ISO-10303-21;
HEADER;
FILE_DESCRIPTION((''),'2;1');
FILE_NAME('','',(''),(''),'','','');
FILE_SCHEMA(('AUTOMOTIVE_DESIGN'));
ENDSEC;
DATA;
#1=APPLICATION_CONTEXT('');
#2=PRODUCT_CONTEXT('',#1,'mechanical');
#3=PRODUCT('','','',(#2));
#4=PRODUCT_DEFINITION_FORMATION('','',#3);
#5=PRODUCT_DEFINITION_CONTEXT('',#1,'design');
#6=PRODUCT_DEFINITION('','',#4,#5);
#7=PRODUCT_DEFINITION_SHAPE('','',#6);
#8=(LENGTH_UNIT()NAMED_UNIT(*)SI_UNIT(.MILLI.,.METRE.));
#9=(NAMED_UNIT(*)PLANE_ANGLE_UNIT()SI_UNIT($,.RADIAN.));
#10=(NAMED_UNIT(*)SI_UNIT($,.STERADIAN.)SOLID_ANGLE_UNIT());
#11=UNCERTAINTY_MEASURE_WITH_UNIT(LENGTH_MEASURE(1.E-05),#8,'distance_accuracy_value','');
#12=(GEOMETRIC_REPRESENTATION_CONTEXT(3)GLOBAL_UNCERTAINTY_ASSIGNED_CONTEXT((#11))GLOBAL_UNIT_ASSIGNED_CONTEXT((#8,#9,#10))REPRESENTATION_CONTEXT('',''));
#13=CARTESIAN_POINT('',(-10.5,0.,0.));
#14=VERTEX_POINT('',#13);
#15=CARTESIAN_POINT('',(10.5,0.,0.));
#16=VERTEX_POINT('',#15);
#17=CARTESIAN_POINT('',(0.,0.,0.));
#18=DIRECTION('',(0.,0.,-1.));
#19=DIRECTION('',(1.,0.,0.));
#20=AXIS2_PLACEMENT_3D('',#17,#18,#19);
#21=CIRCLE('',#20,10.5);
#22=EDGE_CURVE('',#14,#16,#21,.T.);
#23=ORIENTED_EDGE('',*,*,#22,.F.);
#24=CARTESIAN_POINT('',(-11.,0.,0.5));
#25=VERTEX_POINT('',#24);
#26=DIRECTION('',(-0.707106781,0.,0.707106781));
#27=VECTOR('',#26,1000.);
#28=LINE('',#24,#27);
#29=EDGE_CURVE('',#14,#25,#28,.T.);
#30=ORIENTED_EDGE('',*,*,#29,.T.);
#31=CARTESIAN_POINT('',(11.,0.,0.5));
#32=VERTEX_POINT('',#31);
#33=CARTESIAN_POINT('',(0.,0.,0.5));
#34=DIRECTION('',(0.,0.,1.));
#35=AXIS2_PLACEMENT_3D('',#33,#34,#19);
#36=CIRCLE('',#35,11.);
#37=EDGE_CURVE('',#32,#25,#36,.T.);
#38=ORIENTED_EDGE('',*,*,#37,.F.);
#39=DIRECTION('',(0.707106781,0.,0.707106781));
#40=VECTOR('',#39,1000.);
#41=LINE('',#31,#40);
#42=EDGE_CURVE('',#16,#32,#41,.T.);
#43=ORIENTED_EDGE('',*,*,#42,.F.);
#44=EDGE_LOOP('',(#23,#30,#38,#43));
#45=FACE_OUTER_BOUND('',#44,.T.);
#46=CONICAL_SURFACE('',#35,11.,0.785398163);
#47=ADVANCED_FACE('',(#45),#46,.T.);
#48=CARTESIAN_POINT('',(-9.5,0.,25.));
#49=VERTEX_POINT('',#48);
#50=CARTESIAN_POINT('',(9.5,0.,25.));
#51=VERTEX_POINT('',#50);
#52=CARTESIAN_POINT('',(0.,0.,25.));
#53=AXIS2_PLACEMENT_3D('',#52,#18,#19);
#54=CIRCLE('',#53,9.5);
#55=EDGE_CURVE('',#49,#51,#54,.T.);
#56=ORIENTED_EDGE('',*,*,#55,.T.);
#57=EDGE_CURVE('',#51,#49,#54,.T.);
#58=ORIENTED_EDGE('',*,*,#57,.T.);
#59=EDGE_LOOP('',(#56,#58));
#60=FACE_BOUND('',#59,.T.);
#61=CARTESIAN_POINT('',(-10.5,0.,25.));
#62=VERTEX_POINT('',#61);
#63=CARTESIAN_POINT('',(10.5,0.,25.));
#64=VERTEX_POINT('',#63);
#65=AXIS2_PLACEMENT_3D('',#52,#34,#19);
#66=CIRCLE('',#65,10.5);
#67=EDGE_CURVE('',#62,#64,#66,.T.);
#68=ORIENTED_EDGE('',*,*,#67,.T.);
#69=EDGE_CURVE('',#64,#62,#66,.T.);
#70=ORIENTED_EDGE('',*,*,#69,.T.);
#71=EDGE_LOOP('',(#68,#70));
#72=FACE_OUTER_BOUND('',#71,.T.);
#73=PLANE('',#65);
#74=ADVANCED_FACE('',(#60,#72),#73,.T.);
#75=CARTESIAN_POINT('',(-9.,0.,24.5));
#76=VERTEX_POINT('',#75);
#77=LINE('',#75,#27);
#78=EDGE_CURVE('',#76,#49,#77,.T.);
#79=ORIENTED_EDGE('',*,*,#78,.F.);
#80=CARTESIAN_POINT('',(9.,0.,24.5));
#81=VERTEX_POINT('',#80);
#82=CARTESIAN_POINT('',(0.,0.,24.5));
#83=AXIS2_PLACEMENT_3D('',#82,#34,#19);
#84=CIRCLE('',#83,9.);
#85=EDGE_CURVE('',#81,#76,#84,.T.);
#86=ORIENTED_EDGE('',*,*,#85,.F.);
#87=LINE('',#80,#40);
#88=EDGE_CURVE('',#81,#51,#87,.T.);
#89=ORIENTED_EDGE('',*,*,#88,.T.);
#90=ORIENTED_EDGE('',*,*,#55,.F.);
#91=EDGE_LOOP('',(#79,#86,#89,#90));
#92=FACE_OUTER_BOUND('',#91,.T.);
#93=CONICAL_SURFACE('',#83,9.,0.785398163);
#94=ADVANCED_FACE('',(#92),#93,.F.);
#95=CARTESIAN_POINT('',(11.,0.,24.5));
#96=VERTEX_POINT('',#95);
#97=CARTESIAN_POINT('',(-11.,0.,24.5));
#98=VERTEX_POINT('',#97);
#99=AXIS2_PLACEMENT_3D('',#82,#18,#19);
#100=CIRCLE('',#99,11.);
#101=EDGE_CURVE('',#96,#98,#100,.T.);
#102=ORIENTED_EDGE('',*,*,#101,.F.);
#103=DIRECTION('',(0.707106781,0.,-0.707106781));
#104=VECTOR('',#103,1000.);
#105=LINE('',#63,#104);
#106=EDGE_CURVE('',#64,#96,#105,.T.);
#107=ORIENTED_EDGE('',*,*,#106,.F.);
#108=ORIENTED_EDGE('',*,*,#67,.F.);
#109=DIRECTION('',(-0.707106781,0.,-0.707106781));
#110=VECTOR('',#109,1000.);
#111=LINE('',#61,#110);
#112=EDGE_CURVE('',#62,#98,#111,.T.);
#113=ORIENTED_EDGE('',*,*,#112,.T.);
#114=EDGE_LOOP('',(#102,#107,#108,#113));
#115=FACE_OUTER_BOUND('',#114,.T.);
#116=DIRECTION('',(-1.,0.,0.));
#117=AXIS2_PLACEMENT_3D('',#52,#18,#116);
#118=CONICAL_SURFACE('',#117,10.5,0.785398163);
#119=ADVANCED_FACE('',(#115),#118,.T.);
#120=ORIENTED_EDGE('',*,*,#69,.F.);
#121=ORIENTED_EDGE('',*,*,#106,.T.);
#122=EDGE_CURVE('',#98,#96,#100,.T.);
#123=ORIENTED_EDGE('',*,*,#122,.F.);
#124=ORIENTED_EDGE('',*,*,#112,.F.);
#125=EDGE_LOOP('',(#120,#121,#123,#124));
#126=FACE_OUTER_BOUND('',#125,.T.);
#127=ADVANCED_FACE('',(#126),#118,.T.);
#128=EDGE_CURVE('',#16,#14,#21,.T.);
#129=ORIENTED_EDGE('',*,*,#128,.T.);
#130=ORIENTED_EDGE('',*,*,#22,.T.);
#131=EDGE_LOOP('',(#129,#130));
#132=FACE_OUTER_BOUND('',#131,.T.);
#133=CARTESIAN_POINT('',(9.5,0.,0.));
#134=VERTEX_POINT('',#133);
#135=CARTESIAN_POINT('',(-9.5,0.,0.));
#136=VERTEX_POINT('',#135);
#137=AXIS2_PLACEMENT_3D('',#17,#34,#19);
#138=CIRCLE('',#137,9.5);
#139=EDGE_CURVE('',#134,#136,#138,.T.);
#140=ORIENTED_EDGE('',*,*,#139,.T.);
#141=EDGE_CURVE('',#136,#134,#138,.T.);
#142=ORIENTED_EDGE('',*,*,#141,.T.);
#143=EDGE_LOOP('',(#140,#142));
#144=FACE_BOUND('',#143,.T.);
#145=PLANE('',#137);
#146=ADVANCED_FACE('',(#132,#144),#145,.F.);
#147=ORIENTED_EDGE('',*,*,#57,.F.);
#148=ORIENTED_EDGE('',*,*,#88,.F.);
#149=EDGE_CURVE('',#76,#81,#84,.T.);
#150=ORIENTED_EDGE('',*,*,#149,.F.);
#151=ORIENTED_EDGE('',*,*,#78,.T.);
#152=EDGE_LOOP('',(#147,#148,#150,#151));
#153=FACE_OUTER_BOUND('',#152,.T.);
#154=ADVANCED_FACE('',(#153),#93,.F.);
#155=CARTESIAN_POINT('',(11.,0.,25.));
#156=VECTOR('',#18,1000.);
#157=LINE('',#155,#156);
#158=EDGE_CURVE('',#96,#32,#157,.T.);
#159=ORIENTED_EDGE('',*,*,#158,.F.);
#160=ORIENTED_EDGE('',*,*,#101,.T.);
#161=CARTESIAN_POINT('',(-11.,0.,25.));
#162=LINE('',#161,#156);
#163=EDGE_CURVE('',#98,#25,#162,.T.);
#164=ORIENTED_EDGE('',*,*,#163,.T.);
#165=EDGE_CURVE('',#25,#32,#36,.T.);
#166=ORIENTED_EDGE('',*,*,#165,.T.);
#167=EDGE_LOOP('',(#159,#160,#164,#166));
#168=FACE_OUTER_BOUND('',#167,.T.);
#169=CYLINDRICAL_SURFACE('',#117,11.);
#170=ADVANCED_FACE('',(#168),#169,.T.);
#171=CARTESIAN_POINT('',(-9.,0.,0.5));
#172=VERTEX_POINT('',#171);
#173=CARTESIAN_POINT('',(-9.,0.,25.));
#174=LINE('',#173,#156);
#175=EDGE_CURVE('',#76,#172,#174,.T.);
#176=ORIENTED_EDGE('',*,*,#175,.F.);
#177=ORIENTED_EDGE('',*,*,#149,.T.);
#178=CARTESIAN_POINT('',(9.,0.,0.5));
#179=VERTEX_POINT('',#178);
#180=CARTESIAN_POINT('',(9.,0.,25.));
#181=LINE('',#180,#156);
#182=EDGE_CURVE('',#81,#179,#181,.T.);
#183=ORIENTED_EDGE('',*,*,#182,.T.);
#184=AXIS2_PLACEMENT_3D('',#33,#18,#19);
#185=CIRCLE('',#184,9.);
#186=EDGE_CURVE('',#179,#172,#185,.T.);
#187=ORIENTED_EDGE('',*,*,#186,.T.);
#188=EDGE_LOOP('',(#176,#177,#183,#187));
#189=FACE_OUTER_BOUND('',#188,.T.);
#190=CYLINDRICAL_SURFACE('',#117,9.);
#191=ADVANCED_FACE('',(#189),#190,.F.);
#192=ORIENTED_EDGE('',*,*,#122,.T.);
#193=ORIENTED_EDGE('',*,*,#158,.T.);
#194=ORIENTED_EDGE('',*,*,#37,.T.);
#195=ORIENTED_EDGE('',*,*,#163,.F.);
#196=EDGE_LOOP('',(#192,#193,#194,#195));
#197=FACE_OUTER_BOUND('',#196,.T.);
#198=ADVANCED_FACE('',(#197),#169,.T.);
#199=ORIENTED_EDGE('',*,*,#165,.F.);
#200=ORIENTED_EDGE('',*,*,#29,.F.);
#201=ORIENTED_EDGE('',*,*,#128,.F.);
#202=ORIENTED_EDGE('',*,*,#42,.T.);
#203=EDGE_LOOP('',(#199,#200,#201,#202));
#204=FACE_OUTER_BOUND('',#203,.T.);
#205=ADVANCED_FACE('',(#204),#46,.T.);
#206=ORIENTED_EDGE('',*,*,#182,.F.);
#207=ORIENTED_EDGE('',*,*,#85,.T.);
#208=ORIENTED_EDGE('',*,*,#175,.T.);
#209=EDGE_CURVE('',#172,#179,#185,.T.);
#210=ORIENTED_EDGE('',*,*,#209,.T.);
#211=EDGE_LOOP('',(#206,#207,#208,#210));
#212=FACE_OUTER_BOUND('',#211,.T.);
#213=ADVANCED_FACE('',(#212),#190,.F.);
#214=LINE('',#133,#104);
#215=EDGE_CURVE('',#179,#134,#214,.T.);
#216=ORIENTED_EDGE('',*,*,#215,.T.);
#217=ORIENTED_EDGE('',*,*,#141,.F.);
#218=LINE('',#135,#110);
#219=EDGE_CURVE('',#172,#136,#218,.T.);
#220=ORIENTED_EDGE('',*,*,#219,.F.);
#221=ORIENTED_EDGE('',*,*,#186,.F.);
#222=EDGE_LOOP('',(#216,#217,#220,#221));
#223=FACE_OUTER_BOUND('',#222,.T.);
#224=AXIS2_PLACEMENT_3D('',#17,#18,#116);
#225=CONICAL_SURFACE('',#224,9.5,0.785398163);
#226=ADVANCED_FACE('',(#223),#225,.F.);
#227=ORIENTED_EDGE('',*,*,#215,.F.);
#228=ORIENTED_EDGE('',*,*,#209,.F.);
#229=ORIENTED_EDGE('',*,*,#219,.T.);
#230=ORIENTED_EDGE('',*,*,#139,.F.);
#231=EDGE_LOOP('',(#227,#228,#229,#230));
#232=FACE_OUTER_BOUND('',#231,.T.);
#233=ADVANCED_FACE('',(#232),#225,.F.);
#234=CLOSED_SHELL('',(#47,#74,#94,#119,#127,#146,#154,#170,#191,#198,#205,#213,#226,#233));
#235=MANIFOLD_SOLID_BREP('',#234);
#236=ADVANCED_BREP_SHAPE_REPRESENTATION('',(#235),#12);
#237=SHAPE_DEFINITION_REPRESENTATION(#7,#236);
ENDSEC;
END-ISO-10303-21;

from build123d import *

# Parameters (mm, degrees)
SKETCH_1_R      = 11
SKETCH_1_R_2    = 9
EXTRUDE_1_DEPTH = 25
CHAMFER_1_SIZE  = 0.5


with BuildPart() as part:
    # 草图1 → 凸台-拉伸1 (new body)
    with BuildSketch(Plane.XY):
        Circle(SKETCH_1_R)
        Circle(SKETCH_1_R_2, mode=Mode.SUBTRACT)
    extrude(amount=EXTRUDE_1_DEPTH)

    # 倒角1
    chamfer_1_edges = [part.edges().sort_by_distance(p)[0] for p in [
        (-11, 0, 0),
        (-11, 0, 25),
        (-9, 0, 0),
        (-9, 0, 25),
    ]]
    chamfer(chamfer_1_edges, length=CHAMFER_1_SIZE)


solid = part.part
